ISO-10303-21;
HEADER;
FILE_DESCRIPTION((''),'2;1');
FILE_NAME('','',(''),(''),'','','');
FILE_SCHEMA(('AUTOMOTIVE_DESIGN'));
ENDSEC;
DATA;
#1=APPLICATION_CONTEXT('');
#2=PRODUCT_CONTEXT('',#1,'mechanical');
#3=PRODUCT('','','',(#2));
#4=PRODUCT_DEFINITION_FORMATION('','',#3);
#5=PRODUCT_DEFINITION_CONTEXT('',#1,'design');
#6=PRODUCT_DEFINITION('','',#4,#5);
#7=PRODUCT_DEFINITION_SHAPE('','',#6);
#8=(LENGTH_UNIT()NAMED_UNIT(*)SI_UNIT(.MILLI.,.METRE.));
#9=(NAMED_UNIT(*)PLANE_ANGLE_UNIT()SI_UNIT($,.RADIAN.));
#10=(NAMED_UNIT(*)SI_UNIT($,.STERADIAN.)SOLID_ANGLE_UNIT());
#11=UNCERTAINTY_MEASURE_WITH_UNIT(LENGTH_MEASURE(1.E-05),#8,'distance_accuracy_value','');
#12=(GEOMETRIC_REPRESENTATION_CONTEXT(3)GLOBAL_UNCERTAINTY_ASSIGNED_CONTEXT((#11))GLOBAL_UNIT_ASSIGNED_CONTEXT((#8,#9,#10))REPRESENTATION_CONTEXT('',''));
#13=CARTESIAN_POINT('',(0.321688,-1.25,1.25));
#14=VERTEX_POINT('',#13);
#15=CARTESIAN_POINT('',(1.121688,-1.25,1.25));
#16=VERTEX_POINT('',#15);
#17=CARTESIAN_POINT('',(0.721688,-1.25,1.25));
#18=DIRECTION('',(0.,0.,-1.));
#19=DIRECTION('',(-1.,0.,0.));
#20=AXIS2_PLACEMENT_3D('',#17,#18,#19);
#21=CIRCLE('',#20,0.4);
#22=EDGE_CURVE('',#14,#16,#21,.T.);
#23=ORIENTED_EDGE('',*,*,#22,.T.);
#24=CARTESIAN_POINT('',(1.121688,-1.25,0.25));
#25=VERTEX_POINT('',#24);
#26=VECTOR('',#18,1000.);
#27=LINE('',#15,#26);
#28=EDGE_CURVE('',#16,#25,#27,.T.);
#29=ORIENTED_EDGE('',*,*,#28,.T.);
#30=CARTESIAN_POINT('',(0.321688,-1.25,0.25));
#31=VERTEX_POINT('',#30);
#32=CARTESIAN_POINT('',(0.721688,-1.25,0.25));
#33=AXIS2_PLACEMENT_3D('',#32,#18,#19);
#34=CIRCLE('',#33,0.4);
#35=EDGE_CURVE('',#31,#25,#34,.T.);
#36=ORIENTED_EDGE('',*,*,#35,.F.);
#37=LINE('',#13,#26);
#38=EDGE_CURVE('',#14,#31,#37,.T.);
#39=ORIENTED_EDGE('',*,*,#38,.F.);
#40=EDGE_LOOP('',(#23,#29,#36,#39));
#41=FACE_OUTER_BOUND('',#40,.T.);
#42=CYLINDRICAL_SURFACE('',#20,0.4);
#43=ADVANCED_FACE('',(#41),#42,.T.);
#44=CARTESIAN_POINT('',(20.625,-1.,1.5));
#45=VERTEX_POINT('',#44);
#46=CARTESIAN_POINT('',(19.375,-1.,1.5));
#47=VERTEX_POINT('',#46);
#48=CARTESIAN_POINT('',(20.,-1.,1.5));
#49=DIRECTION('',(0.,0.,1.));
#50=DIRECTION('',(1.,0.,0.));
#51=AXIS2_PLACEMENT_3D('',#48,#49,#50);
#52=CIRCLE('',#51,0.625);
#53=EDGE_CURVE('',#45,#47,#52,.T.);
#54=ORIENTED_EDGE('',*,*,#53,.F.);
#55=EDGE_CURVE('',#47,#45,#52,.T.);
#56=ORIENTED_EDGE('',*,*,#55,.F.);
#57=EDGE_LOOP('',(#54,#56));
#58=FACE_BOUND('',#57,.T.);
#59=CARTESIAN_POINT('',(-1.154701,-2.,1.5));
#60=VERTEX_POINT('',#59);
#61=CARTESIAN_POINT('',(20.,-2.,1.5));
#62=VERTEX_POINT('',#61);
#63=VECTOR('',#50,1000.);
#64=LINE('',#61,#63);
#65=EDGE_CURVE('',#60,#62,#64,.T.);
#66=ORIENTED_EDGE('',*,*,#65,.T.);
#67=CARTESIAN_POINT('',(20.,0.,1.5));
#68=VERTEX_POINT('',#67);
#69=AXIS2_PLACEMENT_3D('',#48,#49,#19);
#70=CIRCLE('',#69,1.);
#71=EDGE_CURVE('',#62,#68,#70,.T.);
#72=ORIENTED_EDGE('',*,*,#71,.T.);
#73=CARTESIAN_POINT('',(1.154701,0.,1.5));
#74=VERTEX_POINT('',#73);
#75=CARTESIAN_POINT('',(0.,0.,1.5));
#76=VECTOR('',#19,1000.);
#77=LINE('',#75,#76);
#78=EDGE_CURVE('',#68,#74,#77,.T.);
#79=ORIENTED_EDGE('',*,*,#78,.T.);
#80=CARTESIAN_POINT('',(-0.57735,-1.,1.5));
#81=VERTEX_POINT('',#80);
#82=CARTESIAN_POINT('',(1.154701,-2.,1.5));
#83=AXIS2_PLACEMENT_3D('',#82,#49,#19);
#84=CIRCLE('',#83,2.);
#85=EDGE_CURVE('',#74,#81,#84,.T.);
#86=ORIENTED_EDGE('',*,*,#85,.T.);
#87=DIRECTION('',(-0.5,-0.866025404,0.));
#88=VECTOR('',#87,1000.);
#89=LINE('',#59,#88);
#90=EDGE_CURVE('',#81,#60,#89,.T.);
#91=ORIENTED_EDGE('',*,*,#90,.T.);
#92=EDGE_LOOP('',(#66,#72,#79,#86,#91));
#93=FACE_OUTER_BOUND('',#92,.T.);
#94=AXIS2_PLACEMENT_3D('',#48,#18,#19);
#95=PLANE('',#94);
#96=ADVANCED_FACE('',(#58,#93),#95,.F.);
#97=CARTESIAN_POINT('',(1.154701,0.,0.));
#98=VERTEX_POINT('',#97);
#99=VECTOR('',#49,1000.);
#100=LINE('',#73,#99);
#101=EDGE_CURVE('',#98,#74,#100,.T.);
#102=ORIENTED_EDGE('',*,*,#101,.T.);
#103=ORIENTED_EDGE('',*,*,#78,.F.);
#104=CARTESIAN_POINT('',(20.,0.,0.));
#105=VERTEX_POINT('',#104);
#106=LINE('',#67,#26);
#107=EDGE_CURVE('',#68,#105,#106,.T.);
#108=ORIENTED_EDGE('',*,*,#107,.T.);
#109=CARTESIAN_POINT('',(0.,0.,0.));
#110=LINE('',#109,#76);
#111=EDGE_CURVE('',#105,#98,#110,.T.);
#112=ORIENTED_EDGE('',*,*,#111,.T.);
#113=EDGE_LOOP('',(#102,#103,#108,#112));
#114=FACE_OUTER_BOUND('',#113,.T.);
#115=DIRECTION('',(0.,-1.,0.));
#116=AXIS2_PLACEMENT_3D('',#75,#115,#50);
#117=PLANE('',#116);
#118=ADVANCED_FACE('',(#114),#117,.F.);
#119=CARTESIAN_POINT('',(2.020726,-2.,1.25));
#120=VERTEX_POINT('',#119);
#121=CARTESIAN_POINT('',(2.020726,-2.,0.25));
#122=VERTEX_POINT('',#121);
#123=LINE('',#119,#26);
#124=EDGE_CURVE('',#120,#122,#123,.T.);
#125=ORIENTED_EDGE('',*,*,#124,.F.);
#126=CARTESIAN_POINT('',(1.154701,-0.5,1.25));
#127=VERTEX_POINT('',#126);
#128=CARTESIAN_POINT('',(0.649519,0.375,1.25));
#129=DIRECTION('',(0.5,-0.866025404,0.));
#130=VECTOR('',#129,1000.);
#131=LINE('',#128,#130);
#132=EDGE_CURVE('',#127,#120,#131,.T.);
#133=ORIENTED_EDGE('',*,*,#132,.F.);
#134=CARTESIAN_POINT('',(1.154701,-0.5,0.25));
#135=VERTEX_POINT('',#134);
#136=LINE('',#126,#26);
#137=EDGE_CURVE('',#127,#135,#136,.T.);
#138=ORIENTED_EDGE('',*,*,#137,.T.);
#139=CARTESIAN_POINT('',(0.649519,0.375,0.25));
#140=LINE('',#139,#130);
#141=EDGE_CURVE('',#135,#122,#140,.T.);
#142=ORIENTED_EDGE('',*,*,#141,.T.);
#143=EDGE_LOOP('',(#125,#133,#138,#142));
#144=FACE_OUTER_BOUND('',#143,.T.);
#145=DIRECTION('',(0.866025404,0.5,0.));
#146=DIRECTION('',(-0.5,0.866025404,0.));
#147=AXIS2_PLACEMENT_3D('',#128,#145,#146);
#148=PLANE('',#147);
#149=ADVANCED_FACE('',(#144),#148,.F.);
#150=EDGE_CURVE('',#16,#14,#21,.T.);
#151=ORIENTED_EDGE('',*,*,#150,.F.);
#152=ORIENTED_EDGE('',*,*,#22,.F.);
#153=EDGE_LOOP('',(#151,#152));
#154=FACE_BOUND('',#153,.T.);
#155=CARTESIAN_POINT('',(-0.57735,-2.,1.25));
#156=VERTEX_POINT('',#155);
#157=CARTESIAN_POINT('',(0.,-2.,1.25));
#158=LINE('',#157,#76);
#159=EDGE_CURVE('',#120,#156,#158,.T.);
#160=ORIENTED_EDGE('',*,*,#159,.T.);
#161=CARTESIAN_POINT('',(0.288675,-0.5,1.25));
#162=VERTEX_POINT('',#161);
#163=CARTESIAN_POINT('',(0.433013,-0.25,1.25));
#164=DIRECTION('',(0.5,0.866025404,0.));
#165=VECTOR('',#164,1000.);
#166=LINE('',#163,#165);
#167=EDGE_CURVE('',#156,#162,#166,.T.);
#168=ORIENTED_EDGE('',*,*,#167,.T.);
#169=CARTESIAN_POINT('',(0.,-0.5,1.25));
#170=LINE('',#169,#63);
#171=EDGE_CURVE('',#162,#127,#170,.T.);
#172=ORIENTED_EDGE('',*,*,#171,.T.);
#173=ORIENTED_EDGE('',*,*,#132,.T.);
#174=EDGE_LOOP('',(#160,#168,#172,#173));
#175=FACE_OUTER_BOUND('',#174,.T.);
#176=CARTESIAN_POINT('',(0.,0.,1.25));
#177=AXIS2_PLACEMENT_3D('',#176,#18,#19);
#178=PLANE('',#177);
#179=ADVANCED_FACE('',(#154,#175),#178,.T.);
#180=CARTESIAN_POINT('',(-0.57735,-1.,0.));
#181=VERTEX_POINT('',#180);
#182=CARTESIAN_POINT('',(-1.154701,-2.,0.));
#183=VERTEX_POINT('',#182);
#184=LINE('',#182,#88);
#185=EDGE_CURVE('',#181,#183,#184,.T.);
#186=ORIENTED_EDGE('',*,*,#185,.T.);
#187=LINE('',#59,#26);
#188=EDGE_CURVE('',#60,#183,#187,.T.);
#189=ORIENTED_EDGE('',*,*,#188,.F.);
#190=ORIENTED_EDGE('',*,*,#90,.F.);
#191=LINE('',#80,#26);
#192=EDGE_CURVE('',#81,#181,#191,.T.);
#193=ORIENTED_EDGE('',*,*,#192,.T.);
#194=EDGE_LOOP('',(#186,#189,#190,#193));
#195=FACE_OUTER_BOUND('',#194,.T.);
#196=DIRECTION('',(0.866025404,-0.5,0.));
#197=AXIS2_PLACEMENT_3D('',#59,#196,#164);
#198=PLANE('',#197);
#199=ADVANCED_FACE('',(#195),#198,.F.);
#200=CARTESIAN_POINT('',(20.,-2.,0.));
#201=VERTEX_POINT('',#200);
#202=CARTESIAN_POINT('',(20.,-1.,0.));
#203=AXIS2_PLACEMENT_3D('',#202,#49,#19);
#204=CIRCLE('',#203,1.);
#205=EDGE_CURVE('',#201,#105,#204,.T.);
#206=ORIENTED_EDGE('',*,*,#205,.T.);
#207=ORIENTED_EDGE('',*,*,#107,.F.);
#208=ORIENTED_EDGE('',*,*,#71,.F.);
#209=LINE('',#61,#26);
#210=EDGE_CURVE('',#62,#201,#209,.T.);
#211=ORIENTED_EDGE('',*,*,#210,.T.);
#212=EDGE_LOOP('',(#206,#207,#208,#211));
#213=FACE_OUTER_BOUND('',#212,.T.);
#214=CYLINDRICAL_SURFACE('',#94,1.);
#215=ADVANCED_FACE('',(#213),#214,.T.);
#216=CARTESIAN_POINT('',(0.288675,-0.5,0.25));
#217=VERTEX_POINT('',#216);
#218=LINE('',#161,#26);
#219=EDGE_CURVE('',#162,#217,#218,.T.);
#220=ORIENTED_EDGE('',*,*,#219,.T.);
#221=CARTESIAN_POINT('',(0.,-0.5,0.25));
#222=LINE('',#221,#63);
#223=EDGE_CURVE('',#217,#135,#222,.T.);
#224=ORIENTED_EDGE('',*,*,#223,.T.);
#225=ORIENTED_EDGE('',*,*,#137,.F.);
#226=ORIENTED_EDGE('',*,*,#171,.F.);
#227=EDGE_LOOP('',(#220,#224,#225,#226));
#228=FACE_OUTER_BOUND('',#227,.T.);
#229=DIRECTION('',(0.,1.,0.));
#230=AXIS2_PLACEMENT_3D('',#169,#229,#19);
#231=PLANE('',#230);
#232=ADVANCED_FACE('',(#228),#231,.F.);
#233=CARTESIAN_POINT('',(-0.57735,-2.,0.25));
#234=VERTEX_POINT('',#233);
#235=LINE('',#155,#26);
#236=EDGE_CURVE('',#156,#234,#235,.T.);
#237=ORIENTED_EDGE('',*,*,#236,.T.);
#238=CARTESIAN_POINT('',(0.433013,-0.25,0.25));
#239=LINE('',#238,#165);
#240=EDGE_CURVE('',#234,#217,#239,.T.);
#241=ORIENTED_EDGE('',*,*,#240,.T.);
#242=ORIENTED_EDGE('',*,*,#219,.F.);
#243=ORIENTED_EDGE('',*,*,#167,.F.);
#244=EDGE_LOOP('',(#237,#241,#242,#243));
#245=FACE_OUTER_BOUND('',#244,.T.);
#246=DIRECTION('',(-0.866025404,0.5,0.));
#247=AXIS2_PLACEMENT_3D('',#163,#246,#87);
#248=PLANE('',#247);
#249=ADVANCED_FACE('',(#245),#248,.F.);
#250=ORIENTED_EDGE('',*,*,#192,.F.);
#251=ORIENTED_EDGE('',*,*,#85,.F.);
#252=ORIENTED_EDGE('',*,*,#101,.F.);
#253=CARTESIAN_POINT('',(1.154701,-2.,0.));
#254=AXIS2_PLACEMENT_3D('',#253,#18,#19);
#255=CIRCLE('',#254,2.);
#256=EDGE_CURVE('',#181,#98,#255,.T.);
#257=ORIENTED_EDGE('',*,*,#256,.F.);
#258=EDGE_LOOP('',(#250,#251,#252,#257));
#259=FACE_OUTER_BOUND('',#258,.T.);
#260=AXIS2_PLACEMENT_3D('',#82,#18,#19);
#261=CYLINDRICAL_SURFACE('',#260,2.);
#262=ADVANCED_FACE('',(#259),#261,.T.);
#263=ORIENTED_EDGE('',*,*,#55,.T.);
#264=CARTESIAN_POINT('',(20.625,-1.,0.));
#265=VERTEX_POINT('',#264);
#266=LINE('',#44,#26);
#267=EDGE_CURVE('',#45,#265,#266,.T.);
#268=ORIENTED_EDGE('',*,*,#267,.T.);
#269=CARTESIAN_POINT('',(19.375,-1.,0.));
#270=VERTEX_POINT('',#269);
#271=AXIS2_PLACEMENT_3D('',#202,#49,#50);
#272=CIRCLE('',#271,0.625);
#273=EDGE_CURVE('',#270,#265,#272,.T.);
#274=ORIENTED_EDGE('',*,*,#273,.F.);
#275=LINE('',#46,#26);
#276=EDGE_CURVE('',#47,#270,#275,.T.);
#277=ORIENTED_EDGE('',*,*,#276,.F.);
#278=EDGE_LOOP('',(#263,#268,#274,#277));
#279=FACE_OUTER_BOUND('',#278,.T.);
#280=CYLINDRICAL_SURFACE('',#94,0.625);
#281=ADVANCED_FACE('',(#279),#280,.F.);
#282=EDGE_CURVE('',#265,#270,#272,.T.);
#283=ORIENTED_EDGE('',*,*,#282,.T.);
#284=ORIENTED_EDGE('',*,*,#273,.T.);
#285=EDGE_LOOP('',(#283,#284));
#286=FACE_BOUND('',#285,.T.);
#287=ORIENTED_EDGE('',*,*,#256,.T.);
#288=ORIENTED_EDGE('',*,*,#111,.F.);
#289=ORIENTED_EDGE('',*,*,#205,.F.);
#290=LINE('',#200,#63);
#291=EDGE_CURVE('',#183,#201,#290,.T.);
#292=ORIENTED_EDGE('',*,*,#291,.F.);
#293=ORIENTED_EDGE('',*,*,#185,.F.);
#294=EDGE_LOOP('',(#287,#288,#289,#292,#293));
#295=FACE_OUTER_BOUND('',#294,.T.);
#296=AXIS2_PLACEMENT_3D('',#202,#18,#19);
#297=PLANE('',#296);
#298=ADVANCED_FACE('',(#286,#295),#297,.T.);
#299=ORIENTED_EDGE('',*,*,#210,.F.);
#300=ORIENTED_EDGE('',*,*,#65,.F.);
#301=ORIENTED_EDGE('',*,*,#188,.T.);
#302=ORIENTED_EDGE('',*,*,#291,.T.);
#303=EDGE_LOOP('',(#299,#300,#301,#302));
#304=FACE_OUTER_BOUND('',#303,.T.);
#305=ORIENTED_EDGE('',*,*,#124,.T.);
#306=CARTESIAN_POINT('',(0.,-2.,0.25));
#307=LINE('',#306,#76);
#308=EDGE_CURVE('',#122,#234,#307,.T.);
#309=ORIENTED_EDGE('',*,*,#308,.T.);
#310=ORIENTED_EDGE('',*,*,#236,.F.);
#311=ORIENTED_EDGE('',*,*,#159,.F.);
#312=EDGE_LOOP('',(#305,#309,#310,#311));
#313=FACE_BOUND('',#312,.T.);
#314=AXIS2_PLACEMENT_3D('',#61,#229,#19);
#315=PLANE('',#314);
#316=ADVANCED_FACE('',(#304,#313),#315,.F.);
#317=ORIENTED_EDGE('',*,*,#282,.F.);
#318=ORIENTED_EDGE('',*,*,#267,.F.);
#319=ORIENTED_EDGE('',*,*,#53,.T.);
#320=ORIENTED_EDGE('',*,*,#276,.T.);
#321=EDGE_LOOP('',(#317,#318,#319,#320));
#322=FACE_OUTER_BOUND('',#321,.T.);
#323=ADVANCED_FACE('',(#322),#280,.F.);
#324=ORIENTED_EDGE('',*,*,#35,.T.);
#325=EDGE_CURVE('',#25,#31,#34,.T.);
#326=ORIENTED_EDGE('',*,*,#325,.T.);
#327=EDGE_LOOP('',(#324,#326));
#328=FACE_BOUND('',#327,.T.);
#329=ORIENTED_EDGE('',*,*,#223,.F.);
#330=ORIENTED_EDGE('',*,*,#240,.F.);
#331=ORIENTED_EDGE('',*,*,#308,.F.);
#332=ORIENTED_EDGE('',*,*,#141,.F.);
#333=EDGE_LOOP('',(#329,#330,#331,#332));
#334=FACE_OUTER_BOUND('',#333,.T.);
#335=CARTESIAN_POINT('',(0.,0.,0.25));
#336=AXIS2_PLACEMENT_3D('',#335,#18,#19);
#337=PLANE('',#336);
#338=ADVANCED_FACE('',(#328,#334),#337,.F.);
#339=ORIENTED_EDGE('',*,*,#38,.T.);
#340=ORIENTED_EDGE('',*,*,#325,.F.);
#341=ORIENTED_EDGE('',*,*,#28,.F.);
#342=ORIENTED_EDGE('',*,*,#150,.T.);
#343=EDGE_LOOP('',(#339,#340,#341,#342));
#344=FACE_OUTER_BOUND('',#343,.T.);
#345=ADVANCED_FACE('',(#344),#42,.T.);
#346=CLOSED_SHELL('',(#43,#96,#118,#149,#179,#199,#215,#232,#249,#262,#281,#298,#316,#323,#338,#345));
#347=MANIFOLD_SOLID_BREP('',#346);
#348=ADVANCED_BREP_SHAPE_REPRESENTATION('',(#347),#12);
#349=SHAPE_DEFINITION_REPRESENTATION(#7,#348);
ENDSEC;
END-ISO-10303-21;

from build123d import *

# Parameters (mm, degrees)
SKETCH1_R           = 0.625
BOSS_EXTRUDE2_DEPTH = 1.5
SKETCH3_R           = 0.75
SKETCH3_R_2         = 0.4
CUT_EXTRUDE1_DEPTH  = 0.5
FILLET1_R           = 2


with BuildPart() as part:
    # Sketch1 → Boss-Extrude2 (new body)
    with BuildSketch(Plane.XY):
        with BuildLine():
            Line((0, 0), (20, 0))
            ThreePointArc((20, 0), (21, -1), (20, -2))
            Line((20, -2), (-1.154700538, -2))
            Line((-1.154700538, -2), (0, 0))
        make_face()
        with Locations((20, -1)):
            Circle(SKETCH1_R, mode=Mode.SUBTRACT)
    extrude(amount=BOSS_EXTRUDE2_DEPTH)

    # Sketch3 → Cut-Extrude1 (cut, symmetric)
    # profile 1 of 5: a face of its own
    with BuildSketch(Plane(origin=(0, 0, 0.75), x_dir=(-1, 0, 0), z_dir=(0, 0, -1))):
        with BuildLine():
            ThreePointArc((-1.371206885, -0.874999993), (-1.096687833, -0.600480945), (-0.721687836, -0.5))
            Line((-0.721687836, -0.5), (-1.154700538, -0.5))
            Line((-1.154700538, -0.5), (-1.371206885, -0.874999993))
        make_face()
    # profile 2 of 5: a face of its own
    with BuildSketch(Plane(origin=(0, 0, 0.75), x_dir=(-1, 0, 0), z_dir=(0, 0, -1))):
        with BuildLine():
            ThreePointArc((-0.721687836, -0.5), (-0.346687831, -0.60048095), (-0.072168777, -0.875000011))
            Line((-0.072168777, -0.875000011), (-0.288675135, -0.5))
            Line((-0.288675135, -0.5), (-0.721687836, -0.5))
        make_face()
    # profile 3 of 5: a face of its own
    with BuildSketch(Plane(origin=(0, 0, 0.75), x_dir=(-1, 0, 0), z_dir=(0, 0, -1))):
        with BuildLine():
            Line((-0.721687836, -2), (0.577350269, -2))
            Line((0.577350269, -2), (-0.072168777, -0.875000011))
            ThreePointArc((-0.072168777, -0.875000011), (0.002756535, -1.055885722), (0.028312164, -1.25))
            ThreePointArc((0.028312164, -1.25), (-0.191357751, -1.780330086), (-0.721687836, -2))
        make_face()
    # profile 4 of 5: a face of its own
    with BuildSketch(Plane(origin=(0, 0, 0.75), x_dir=(-1, 0, 0), z_dir=(0, 0, -1))):
        with BuildLine():
            Line((-2.020725942, -2), (-0.721687836, -2))
            ThreePointArc((-0.721687836, -2), (-1.371206891, -1.624999997), (-1.371206885, -0.874999993))
            Line((-1.371206885, -0.874999993), (-2.020725942, -2))
        make_face()
    # profile 5 of 5: a face of its own
    with BuildSketch(Plane(origin=(0, 0, 0.75), x_dir=(-1, 0, 0), z_dir=(0, 0, -1))):
        with Locations((-0.721687836, -1.25)):
            Circle(SKETCH3_R)
        with Locations((-0.721687836, -1.25)):
            Circle(SKETCH3_R_2, mode=Mode.SUBTRACT)
    extrude(amount=CUT_EXTRUDE1_DEPTH, both=True, mode=Mode.SUBTRACT)

    # Fillet1
    fillet1_edges = [part.edges().sort_by_distance(p)[0] for p in [
        (0, 0, 0.75),
    ]]
    fillet(fillet1_edges, radius=FILLET1_R)


solid = part.part
